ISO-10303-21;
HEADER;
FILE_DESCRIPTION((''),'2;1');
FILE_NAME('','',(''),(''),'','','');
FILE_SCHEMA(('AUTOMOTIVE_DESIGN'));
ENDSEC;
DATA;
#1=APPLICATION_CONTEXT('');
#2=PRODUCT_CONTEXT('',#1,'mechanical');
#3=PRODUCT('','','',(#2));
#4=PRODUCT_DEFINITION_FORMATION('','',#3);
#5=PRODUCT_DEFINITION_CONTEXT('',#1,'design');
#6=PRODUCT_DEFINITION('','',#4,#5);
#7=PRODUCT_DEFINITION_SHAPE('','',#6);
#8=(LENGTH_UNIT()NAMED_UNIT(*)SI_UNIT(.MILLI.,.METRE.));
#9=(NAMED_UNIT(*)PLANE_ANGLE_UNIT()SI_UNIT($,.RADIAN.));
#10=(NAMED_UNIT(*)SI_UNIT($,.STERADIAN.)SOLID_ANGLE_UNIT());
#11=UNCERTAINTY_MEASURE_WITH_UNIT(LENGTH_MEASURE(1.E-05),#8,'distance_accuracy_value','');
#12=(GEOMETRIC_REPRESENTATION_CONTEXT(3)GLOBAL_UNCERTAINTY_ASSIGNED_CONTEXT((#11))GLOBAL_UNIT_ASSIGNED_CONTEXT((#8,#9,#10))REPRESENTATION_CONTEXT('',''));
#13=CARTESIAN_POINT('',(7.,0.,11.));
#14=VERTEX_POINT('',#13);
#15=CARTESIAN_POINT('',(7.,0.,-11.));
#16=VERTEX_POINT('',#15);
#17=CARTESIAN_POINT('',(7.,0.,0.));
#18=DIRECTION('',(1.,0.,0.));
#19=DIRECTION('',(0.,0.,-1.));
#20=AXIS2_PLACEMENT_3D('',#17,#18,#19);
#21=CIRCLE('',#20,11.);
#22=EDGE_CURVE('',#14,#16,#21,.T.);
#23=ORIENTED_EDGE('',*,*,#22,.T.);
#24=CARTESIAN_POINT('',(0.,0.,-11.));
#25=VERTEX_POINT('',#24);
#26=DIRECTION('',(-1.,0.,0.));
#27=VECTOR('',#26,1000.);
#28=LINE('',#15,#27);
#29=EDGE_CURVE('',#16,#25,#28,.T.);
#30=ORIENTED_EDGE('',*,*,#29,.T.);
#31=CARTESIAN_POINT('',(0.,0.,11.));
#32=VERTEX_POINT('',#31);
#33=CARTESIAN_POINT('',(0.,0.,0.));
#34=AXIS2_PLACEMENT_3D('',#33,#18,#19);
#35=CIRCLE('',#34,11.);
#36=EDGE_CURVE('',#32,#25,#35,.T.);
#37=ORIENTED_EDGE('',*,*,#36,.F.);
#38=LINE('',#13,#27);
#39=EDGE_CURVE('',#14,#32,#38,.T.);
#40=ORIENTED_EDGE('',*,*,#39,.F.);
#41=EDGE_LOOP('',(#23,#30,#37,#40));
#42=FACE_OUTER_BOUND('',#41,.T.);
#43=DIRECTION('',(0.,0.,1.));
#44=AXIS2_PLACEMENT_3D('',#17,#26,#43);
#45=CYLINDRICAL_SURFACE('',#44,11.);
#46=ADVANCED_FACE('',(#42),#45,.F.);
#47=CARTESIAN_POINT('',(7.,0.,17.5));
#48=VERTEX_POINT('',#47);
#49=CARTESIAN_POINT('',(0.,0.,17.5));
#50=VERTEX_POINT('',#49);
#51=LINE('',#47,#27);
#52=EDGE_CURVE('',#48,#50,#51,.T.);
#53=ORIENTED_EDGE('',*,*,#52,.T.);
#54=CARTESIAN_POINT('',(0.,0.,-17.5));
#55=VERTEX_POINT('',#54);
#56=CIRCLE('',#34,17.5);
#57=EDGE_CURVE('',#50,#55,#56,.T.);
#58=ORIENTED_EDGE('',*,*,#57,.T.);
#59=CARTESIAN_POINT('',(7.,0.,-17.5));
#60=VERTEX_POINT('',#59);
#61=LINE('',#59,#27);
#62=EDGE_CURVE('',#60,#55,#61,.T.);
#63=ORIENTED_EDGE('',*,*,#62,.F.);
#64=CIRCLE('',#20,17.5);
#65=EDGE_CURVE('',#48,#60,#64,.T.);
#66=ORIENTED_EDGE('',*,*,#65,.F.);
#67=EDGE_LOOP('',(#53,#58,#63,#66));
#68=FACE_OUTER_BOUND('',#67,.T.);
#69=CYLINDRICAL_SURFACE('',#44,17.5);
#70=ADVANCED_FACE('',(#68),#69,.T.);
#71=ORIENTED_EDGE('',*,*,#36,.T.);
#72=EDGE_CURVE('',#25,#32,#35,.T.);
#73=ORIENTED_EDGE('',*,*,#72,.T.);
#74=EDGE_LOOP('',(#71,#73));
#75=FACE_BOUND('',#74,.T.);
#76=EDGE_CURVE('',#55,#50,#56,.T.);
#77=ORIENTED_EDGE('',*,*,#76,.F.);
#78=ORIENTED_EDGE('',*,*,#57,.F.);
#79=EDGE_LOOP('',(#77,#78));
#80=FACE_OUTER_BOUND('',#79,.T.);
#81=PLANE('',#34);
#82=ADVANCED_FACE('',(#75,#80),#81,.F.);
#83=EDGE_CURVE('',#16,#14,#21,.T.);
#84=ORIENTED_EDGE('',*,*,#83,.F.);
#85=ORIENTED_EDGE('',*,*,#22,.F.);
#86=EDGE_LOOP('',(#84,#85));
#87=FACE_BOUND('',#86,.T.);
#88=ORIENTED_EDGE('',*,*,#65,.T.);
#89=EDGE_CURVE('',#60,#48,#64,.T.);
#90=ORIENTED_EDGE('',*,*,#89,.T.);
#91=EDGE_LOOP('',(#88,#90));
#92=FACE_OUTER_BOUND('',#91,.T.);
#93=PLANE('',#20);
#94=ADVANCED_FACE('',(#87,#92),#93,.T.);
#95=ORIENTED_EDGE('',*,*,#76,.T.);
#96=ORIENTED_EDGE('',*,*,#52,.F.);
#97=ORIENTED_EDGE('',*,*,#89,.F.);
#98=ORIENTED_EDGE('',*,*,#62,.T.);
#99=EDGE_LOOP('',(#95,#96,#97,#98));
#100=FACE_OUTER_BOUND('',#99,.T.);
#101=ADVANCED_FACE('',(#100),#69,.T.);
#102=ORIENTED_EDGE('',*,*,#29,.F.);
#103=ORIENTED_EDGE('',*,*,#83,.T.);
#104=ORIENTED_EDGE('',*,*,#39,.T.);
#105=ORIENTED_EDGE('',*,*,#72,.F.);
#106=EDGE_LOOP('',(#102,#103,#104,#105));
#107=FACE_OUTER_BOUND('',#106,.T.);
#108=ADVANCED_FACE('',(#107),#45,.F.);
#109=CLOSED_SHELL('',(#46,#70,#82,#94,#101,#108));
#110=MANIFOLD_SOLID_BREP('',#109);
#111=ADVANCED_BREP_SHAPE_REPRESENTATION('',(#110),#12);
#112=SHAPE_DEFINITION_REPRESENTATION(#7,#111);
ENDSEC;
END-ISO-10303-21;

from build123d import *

# Parameters (mm, degrees)
SKETCH_1_R      = 17.5
SKETCH_1_R_2    = 11
EXTRUDE_1_DEPTH = 7


with BuildPart() as part:
    # 草图1 → 凸台-拉伸1 (new body)
    with BuildSketch(Plane(origin=(0, 0, 0), x_dir=(0, 0, -1), z_dir=(1, 0, 0))):
        Circle(SKETCH_1_R)
        Circle(SKETCH_1_R_2, mode=Mode.SUBTRACT)
    extrude(amount=EXTRUDE_1_DEPTH)


solid = part.part
